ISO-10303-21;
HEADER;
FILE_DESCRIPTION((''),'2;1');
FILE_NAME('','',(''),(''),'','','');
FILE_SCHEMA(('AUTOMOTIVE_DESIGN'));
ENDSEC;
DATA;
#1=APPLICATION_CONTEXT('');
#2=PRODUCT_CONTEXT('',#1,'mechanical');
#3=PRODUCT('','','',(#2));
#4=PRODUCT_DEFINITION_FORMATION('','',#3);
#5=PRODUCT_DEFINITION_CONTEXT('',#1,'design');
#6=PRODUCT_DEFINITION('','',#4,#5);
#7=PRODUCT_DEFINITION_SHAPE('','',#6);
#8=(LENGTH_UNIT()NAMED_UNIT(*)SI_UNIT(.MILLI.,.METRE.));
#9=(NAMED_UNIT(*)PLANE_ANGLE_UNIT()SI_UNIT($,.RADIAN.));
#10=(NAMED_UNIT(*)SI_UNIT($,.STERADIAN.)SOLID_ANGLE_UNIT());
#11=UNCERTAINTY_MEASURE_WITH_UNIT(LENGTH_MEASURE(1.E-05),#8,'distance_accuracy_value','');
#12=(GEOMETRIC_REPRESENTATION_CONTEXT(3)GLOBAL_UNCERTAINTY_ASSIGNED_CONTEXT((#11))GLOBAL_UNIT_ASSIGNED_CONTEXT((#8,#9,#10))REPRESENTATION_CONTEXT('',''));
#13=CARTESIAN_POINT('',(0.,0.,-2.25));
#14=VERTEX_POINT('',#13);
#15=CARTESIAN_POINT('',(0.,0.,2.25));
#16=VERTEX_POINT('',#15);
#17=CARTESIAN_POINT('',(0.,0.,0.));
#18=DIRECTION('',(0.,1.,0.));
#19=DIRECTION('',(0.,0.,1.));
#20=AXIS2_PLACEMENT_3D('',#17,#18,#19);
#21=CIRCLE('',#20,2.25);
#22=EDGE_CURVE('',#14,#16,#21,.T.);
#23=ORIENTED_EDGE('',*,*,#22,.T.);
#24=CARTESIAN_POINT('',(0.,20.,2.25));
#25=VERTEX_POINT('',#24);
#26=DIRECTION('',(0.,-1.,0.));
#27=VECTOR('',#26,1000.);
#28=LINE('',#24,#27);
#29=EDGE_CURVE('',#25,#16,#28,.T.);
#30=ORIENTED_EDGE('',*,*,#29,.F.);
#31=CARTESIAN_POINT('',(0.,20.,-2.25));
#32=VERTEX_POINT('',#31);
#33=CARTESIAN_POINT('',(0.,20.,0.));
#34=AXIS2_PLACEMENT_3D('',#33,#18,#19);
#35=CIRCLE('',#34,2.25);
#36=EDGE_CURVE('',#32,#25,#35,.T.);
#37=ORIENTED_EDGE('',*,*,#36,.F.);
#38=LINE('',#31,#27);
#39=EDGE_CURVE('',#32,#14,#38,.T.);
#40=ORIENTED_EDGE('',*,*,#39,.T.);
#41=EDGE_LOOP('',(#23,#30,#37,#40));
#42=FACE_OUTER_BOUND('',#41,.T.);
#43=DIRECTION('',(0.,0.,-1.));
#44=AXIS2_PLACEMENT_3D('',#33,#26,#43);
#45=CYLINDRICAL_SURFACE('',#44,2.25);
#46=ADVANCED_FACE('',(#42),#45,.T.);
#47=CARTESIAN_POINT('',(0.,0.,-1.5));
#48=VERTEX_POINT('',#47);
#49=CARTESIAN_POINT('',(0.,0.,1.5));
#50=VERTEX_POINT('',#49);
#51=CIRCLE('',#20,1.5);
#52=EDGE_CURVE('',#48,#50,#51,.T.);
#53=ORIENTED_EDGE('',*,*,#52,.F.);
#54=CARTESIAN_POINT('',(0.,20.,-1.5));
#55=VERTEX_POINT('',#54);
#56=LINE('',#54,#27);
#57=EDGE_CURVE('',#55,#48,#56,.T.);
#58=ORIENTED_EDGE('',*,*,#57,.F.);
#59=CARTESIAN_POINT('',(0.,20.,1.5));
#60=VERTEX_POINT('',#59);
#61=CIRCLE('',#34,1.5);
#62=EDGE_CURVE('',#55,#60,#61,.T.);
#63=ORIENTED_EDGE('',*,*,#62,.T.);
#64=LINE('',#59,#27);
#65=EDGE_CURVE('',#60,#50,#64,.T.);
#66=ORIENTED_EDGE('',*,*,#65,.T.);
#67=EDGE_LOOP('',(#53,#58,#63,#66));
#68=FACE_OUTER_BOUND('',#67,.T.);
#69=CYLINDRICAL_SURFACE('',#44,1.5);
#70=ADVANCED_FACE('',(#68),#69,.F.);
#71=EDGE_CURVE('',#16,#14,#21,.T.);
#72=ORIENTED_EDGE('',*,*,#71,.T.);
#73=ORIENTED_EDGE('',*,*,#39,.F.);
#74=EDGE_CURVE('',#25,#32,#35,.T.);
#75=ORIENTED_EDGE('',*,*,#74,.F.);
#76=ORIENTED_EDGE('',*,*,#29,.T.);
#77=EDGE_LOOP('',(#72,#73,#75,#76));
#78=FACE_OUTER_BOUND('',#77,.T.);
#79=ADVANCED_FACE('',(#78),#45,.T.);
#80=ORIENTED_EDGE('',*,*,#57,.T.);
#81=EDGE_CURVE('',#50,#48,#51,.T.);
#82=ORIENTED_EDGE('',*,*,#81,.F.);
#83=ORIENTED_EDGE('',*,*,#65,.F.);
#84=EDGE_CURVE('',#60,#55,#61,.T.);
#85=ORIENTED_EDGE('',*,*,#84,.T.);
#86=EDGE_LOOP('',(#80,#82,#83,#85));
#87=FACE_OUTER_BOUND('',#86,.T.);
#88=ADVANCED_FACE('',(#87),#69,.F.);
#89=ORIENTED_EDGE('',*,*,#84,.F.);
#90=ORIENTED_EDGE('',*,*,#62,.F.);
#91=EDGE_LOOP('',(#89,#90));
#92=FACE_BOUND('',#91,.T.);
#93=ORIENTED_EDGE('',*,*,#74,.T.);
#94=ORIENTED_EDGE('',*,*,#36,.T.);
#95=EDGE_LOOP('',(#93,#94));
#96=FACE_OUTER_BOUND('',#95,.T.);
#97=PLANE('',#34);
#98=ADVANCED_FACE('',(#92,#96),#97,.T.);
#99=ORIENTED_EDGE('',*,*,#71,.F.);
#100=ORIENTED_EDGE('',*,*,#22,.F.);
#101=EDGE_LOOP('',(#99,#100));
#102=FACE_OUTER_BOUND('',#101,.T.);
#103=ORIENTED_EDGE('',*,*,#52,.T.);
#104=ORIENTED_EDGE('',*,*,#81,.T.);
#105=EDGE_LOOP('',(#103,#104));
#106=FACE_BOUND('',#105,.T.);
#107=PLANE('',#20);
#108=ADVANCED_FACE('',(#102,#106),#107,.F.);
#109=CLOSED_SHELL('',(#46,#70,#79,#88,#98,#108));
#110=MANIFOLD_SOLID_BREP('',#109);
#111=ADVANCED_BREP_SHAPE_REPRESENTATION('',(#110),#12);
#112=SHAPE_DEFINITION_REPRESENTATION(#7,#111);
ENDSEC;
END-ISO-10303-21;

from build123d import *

# Parameters (mm, degrees)
SKETCH1_R           = 2.25
SKETCH1_R_2         = 1.5
BOSS_EXTRUDE1_DEPTH = 20


with BuildPart() as part:
    # Sketch1 → Boss-Extrude1 (new body)
    with BuildSketch(Plane(origin=(0, 0, 0), x_dir=(1, 0, 0), z_dir=(0, 1, 0))):
        with Locations(Location((0, 0, 0), (0, 0, 270))):
            Circle(SKETCH1_R)
        with Locations(Location((0, 0, 0), (0, 0, 270))):
            Circle(SKETCH1_R_2, mode=Mode.SUBTRACT)
    extrude(amount=BOSS_EXTRUDE1_DEPTH)


solid = part.part
